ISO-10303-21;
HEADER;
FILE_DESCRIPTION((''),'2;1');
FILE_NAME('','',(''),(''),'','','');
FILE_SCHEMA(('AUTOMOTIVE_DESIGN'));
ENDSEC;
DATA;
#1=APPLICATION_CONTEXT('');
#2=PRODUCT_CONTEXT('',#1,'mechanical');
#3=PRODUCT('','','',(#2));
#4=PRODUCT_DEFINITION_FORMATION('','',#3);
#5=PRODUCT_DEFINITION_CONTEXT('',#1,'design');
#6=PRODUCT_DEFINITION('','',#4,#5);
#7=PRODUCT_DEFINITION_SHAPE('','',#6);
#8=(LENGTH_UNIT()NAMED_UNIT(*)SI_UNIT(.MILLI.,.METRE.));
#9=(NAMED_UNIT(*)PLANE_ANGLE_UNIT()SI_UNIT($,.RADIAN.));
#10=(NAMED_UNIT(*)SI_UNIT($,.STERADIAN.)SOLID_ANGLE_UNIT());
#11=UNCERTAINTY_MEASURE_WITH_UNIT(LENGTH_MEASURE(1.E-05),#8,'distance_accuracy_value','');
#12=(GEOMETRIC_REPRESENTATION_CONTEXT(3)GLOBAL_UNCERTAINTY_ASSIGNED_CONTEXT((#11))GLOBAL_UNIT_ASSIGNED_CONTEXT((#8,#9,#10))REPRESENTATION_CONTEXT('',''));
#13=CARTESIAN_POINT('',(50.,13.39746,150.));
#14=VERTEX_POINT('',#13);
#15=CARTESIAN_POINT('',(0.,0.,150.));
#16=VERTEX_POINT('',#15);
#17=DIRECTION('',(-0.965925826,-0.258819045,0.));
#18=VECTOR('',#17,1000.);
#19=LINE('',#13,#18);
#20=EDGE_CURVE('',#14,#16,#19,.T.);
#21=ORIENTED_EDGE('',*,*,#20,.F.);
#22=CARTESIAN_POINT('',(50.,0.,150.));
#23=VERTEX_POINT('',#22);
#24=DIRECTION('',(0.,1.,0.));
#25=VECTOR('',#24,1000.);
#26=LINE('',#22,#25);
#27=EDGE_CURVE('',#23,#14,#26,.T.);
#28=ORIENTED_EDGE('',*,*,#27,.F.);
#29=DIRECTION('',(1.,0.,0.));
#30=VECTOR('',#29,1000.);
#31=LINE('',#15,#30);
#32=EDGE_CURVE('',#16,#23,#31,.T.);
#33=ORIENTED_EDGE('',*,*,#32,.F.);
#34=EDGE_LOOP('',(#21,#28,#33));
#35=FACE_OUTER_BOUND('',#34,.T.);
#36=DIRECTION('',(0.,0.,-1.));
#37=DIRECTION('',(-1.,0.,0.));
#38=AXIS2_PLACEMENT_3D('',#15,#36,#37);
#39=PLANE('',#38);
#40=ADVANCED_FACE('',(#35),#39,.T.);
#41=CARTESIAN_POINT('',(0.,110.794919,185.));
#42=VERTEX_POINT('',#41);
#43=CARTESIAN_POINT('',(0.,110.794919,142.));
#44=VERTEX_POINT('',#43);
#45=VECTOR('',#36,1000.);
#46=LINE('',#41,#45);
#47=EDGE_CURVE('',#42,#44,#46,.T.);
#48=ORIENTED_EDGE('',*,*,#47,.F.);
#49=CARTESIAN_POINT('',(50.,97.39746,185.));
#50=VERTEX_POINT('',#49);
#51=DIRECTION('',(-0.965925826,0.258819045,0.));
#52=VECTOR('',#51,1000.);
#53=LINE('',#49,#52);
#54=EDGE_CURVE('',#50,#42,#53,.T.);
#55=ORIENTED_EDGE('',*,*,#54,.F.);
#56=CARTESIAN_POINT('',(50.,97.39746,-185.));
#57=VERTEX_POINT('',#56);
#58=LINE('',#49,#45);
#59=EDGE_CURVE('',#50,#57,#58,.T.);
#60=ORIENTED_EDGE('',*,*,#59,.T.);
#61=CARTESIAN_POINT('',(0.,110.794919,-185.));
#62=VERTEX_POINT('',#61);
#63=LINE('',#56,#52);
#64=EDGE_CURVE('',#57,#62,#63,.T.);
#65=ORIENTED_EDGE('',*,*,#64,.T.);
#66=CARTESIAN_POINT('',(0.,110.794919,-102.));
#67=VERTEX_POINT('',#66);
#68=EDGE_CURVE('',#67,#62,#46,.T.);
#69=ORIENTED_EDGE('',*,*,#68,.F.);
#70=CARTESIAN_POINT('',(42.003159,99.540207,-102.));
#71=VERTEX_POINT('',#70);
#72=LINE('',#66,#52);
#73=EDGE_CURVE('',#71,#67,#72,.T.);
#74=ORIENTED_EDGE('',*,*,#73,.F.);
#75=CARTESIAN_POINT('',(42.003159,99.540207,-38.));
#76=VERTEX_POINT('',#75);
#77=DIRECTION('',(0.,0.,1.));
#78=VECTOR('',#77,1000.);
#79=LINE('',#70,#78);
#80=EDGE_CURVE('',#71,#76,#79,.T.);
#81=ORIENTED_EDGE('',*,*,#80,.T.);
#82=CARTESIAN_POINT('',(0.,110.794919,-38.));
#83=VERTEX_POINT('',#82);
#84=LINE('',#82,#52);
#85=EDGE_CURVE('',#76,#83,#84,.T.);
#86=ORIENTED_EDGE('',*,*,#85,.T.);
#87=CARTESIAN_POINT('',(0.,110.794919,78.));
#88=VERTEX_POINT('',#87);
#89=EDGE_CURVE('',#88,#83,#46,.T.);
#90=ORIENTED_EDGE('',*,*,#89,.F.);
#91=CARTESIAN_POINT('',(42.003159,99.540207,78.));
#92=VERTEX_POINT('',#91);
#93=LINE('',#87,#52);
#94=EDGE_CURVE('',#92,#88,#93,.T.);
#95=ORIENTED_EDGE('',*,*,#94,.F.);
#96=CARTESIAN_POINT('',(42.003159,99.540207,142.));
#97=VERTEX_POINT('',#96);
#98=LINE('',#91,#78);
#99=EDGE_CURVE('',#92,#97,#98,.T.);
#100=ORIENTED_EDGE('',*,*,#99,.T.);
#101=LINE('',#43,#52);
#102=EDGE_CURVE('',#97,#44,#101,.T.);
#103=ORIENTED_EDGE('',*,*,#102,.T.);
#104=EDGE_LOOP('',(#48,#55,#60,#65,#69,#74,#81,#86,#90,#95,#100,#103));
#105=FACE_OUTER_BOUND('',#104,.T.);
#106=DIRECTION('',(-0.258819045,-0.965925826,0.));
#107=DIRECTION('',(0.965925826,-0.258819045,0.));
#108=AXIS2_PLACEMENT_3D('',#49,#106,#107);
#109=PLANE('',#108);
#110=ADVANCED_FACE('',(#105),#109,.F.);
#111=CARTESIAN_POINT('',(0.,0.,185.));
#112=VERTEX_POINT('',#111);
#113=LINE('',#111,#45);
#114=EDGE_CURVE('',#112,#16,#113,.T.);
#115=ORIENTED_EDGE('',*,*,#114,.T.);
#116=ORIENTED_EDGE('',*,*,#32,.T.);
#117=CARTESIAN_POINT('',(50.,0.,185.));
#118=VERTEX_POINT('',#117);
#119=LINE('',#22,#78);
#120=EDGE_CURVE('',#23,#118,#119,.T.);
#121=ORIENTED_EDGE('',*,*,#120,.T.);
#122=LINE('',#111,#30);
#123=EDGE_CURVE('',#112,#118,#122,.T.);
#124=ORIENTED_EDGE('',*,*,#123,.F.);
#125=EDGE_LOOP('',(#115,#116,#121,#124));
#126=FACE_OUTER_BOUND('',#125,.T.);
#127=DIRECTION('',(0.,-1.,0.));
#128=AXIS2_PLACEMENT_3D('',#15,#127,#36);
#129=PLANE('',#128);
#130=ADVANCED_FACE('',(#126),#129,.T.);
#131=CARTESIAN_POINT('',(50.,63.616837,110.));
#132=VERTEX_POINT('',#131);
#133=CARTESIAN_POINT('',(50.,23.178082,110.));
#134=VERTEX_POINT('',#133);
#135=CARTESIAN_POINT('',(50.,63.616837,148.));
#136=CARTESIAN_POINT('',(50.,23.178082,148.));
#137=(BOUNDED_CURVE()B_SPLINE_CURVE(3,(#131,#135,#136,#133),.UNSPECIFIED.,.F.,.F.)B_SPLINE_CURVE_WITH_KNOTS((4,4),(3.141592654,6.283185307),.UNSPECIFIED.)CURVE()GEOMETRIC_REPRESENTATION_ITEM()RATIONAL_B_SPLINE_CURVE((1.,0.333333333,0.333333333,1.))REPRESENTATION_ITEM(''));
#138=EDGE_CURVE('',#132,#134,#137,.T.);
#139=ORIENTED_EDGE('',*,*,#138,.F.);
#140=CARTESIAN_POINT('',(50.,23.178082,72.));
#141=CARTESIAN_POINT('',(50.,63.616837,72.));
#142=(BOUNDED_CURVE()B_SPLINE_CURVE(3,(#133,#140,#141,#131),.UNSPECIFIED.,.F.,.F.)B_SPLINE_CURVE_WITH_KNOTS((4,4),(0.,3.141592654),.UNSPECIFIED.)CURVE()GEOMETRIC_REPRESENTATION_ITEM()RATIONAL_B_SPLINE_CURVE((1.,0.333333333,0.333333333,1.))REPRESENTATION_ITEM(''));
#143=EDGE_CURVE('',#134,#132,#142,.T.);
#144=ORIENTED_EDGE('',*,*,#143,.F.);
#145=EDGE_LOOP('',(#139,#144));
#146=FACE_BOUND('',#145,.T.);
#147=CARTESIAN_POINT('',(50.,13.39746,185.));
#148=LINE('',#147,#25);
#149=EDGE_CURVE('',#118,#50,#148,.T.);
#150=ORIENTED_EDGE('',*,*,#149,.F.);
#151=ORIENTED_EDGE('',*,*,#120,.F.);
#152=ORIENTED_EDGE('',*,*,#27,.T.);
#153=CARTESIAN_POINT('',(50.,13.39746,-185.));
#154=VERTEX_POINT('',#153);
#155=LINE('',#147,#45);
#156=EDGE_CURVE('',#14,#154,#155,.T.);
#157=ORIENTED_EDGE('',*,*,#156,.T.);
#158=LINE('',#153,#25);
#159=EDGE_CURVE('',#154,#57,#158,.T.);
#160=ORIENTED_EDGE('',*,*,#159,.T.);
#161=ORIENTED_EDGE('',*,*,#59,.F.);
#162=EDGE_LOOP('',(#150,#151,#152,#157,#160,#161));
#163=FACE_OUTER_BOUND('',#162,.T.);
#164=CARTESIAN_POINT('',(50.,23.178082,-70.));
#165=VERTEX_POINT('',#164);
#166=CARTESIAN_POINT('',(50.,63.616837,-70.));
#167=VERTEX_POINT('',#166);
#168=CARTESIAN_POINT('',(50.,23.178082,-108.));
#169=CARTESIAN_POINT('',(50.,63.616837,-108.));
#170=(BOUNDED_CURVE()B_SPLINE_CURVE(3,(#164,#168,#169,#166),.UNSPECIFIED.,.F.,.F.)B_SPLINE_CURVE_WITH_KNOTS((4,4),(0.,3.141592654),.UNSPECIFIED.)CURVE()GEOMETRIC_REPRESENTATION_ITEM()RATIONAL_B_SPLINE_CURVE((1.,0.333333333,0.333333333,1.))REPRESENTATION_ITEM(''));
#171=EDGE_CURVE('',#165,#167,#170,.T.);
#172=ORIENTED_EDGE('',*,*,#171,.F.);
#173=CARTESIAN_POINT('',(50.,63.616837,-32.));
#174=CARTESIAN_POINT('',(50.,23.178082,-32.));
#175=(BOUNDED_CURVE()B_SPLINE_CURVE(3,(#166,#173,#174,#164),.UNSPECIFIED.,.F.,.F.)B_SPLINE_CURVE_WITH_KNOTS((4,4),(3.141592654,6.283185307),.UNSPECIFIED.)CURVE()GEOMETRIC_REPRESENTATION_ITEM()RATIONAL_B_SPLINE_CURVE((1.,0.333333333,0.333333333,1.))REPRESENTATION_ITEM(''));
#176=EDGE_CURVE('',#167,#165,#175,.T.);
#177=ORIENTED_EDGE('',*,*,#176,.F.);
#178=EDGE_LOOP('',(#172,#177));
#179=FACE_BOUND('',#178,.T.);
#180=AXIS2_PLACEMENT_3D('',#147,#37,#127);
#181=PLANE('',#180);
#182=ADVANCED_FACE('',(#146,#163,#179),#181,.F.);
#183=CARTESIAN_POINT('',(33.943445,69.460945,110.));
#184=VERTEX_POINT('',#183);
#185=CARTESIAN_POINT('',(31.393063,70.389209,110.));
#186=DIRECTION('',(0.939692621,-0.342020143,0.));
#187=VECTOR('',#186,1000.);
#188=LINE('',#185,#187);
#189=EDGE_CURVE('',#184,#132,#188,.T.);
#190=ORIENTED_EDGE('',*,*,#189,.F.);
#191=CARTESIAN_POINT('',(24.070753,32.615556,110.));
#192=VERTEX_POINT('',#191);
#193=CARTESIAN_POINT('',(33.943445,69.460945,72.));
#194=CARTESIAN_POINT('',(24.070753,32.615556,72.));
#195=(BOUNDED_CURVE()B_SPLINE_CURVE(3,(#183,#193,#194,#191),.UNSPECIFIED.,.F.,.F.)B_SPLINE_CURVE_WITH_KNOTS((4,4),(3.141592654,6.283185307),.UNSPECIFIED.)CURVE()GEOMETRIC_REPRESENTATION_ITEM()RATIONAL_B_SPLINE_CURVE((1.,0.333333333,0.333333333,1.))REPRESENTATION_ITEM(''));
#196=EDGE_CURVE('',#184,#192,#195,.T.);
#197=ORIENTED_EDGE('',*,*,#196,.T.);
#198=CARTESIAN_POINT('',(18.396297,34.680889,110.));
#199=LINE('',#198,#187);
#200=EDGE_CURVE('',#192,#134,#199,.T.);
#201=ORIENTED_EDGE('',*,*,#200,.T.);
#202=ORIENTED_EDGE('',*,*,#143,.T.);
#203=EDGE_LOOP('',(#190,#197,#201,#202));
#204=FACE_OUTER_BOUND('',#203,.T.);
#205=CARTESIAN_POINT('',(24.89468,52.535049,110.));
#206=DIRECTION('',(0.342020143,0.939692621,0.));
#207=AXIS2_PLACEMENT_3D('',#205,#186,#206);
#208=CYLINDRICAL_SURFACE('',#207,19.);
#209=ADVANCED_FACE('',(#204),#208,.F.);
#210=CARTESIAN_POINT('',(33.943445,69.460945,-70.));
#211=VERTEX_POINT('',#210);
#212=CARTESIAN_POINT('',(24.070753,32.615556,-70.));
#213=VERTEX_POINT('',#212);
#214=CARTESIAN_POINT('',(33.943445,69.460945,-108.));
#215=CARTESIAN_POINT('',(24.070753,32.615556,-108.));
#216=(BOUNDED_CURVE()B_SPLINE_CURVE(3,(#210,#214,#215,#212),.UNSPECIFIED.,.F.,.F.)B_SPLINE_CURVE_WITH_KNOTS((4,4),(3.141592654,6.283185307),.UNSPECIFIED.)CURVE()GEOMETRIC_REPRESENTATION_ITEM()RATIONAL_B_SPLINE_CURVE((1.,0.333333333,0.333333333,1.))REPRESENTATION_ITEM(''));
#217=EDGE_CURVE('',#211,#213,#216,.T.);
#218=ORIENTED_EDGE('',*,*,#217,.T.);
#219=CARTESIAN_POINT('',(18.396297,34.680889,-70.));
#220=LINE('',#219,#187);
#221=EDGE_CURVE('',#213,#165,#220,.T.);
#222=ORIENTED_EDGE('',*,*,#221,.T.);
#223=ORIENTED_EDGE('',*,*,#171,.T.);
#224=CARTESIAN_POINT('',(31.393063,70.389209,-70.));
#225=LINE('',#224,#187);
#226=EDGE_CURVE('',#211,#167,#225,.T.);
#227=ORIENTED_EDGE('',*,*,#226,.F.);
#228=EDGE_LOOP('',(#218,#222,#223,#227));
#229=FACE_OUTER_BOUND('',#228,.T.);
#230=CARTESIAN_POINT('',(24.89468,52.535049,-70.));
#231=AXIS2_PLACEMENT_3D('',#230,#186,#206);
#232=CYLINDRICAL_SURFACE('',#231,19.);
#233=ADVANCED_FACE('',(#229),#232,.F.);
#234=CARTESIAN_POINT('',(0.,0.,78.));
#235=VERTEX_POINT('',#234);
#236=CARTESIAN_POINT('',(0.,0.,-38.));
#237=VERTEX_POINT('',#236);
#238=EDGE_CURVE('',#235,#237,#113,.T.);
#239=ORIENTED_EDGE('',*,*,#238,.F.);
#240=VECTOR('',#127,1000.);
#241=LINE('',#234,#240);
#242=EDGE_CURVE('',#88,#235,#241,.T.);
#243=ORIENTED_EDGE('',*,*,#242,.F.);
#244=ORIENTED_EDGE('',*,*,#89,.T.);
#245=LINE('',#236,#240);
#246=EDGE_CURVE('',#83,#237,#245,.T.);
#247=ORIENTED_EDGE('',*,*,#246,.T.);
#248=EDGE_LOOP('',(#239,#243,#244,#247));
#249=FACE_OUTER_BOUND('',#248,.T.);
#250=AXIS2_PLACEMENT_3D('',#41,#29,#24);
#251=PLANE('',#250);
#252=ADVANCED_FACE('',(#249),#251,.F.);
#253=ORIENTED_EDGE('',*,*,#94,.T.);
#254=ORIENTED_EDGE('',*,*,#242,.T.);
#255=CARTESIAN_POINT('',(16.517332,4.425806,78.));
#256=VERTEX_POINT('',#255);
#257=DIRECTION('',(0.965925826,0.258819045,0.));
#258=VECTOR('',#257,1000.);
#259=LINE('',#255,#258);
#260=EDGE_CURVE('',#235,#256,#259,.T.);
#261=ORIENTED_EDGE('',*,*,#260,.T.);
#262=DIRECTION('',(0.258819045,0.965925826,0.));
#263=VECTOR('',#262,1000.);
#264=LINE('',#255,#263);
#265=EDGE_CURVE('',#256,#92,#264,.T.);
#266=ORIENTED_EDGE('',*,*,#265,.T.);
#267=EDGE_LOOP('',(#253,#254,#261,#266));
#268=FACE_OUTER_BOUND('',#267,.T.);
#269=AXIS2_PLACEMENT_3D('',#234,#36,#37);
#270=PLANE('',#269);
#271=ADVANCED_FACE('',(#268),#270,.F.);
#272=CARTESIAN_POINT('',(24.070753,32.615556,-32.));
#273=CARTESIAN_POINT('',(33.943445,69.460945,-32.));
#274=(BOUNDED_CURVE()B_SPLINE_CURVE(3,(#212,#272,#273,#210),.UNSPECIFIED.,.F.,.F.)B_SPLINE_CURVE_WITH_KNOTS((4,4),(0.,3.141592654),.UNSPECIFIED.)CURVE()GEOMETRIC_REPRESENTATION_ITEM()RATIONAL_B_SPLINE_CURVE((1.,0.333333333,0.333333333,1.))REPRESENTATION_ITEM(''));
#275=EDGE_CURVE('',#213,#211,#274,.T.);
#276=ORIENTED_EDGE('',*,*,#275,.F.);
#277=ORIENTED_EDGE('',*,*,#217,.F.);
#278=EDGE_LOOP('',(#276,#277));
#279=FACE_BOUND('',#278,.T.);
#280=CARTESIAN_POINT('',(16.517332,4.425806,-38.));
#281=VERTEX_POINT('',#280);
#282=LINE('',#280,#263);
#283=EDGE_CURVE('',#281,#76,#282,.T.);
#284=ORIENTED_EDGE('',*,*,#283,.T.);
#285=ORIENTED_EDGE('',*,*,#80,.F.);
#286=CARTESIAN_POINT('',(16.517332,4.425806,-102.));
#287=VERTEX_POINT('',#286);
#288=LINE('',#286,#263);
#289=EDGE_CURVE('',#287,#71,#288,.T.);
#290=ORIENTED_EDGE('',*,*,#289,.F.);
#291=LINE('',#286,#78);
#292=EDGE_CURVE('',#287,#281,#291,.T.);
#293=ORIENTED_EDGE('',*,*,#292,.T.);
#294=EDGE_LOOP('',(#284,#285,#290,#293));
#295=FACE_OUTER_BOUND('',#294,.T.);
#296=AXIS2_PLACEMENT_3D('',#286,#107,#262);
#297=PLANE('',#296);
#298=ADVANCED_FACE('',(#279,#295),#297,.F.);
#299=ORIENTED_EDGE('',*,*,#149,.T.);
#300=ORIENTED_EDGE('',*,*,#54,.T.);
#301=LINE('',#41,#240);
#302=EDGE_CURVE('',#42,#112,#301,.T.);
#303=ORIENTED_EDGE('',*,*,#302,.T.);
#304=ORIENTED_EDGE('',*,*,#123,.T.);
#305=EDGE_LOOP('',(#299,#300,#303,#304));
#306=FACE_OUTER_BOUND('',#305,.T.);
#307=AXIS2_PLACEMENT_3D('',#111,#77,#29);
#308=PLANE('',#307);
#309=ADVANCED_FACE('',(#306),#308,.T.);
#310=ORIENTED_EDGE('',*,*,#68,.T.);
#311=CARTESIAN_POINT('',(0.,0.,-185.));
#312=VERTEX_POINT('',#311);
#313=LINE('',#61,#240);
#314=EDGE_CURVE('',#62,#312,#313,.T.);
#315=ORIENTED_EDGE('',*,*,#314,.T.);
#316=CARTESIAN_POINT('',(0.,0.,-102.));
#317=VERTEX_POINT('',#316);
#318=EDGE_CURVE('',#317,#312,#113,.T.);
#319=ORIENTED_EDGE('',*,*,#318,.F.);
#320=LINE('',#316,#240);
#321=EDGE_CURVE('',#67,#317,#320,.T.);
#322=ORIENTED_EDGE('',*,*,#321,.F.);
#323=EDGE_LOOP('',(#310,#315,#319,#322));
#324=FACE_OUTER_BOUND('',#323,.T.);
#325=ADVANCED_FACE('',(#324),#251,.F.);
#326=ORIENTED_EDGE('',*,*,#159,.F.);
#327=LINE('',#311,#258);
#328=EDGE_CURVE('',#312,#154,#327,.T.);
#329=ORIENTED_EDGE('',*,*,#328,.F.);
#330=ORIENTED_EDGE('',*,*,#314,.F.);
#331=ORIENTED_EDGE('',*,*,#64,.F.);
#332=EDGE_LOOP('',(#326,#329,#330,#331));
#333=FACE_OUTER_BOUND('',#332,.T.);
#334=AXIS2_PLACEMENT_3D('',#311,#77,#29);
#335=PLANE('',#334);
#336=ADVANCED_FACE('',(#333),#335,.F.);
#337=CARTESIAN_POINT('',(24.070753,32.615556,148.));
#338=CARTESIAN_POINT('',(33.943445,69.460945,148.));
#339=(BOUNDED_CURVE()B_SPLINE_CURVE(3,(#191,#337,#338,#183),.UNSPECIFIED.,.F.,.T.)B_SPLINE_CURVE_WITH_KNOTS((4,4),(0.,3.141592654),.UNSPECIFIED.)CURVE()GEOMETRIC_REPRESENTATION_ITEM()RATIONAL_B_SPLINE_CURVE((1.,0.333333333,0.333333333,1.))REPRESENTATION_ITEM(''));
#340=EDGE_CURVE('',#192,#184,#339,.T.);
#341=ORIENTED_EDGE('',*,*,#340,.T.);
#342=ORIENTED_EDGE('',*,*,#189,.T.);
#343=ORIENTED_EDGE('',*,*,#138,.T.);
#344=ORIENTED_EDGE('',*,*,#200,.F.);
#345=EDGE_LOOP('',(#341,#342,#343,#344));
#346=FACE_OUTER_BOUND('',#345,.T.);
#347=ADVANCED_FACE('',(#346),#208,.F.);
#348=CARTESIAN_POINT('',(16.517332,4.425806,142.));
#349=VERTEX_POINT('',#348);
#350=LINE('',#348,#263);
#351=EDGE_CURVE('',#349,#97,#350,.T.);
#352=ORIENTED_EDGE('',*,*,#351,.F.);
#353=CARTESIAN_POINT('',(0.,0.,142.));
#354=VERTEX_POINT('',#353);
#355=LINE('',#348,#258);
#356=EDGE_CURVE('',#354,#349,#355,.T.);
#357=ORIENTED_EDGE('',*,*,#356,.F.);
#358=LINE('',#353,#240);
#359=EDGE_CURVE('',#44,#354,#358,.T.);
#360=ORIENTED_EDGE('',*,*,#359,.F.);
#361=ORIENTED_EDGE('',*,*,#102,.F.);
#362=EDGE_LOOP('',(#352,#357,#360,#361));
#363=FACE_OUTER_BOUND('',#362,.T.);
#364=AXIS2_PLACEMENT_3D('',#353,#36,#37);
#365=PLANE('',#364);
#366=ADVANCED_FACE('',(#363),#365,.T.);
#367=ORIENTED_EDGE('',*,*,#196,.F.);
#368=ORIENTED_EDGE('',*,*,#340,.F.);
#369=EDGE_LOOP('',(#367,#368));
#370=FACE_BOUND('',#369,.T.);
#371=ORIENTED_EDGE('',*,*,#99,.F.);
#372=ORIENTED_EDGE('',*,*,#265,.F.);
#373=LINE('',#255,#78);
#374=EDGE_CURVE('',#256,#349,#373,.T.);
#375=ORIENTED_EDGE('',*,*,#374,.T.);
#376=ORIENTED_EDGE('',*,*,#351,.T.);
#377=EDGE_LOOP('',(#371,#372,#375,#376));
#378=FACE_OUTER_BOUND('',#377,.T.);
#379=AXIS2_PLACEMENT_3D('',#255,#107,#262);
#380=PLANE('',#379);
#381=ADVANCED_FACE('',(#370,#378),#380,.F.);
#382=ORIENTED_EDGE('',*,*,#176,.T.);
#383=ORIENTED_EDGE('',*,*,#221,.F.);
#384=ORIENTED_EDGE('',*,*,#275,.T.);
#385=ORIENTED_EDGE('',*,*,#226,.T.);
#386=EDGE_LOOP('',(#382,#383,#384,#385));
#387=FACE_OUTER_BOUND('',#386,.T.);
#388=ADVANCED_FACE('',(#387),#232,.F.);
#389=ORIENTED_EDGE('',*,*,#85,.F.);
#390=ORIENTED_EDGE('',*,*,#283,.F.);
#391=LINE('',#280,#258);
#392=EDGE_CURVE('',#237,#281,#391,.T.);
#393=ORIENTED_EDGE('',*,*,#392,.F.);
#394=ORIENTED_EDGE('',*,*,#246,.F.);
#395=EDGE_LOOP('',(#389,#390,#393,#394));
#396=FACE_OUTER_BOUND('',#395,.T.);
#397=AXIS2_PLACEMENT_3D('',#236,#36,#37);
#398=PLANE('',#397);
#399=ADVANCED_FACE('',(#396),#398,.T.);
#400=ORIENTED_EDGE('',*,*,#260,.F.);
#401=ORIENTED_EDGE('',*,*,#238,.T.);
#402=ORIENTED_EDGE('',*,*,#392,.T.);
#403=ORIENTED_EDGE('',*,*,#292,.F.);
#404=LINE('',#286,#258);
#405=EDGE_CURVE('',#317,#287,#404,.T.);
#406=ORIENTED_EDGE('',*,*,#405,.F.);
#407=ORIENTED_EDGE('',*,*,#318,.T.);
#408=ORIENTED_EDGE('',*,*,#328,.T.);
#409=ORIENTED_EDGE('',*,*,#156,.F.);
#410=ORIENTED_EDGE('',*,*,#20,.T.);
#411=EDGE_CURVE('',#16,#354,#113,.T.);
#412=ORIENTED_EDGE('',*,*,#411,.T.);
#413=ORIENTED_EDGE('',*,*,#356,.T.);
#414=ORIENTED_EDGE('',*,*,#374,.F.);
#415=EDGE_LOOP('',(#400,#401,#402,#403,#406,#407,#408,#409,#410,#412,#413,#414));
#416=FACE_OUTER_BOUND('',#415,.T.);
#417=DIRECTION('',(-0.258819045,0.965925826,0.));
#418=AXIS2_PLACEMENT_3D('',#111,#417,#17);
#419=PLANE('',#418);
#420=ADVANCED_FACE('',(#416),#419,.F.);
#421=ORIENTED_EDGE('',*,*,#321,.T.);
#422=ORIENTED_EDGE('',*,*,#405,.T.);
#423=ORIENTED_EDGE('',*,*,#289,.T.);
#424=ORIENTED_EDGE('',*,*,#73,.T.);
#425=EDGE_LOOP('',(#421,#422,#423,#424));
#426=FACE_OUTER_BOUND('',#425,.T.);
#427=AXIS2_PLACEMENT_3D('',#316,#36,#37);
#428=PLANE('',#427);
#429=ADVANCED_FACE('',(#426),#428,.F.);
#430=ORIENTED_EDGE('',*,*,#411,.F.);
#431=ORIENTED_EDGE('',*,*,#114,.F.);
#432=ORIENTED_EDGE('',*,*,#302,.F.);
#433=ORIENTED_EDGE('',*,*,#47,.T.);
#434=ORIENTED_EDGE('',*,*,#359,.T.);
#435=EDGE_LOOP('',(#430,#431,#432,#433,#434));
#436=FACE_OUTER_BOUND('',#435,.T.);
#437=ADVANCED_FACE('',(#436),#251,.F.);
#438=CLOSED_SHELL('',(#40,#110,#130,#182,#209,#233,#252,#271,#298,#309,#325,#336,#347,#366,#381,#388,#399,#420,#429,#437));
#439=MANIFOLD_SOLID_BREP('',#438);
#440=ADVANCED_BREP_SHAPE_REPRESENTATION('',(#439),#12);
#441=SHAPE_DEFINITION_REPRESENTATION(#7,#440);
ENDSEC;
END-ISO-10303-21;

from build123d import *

# Parameters (mm, degrees)
BOSS_EXTRUDE1_DEPTH = 185
BOSS_EXTRUDE2_DEPTH = 35
CUT_EXTRUDE1_START  = 110
CUT_EXTRUDE1_DEPTH  = 32
CUT_EXTRUDE2_START  = -70
CUT_EXTRUDE2_DEPTH  = 32
SKETCH8_W           = 82.186037081
SKETCH8_H           = 19
LPATTERN1_COUNT     = 2
LPATTERN1_PITCH     = 180


with BuildPart() as part:
    # Sketch1 → Boss-Extrude1 (new, symmetric)
    with BuildSketch(Plane.XY):
        Polygon((0, 0), (50, 13.397459622), (50, 97.397459622), (0, 110.794919243), align=None)
    extrude(amount=BOSS_EXTRUDE1_DEPTH, both=True)

    # Sketch2 → Boss-Extrude2 (add)
    with BuildSketch(Plane.XY.offset(185)):
        Polygon((0, 0), (50, 0), (50, 13.397459622), align=None)
    extrude(amount=-BOSS_EXTRUDE2_DEPTH)

    # Sketch3 → Cut-Extrude1 (cut, symmetric)
    with BuildSketch(Plane.XY.offset(CUT_EXTRUDE1_START)):
        Polygon((16.51733163, 4.425805671), (42.003158605, 99.540206815), (0, 110.794919243), (0, 0), align=None)
    extrude(amount=CUT_EXTRUDE1_DEPTH, both=True, mode=Mode.SUBTRACT)

    # Sketch4 → Cut-Extrude2 (cut, symmetric)
    with BuildSketch(Plane.XY.offset(CUT_EXTRUDE2_START)):
        Polygon((16.51733163, 4.425805671), (0, 0), (0, 110.794919243), (42.003158605, 99.540206815), align=None)
    extrude(amount=CUT_EXTRUDE2_DEPTH, both=True, mode=Mode.SUBTRACT)

    # Sketch8 → Cut-Revolve1 (revolve, cut)
    with BuildSketch(Plane(origin=(19.79656359, 54.390611447, 0), x_dir=(-0.9396926207859083, 0.3420201433256693, 0), z_dir=(0.3420201433256693, 0.9396926207859083, 0)), mode=Mode.PRIVATE) as cut_revolve1_sk:
        with Locations((-10.891297764, -60.5)):
            Rectangle(SKETCH8_W, SKETCH8_H)
    cut_revolve1 = revolve(cut_revolve1_sk.sketch.rotate(Axis((24.894680211, 52.535048747, -70), (-0.9396926207859082, 0.3420201433256693, 0)), 270), axis=Axis((24.894680211, 52.535048747, -70), (-0.9396926207859082, 0.3420201433256693, 0)), mode=Mode.SUBTRACT)

    # LPattern1: Cut-Revolve1 ×2
    with Locations(*[(0, 0, i * LPATTERN1_PITCH) for i in range(1, LPATTERN1_COUNT)]):
        add(cut_revolve1, mode=Mode.SUBTRACT)


solid = part.part
